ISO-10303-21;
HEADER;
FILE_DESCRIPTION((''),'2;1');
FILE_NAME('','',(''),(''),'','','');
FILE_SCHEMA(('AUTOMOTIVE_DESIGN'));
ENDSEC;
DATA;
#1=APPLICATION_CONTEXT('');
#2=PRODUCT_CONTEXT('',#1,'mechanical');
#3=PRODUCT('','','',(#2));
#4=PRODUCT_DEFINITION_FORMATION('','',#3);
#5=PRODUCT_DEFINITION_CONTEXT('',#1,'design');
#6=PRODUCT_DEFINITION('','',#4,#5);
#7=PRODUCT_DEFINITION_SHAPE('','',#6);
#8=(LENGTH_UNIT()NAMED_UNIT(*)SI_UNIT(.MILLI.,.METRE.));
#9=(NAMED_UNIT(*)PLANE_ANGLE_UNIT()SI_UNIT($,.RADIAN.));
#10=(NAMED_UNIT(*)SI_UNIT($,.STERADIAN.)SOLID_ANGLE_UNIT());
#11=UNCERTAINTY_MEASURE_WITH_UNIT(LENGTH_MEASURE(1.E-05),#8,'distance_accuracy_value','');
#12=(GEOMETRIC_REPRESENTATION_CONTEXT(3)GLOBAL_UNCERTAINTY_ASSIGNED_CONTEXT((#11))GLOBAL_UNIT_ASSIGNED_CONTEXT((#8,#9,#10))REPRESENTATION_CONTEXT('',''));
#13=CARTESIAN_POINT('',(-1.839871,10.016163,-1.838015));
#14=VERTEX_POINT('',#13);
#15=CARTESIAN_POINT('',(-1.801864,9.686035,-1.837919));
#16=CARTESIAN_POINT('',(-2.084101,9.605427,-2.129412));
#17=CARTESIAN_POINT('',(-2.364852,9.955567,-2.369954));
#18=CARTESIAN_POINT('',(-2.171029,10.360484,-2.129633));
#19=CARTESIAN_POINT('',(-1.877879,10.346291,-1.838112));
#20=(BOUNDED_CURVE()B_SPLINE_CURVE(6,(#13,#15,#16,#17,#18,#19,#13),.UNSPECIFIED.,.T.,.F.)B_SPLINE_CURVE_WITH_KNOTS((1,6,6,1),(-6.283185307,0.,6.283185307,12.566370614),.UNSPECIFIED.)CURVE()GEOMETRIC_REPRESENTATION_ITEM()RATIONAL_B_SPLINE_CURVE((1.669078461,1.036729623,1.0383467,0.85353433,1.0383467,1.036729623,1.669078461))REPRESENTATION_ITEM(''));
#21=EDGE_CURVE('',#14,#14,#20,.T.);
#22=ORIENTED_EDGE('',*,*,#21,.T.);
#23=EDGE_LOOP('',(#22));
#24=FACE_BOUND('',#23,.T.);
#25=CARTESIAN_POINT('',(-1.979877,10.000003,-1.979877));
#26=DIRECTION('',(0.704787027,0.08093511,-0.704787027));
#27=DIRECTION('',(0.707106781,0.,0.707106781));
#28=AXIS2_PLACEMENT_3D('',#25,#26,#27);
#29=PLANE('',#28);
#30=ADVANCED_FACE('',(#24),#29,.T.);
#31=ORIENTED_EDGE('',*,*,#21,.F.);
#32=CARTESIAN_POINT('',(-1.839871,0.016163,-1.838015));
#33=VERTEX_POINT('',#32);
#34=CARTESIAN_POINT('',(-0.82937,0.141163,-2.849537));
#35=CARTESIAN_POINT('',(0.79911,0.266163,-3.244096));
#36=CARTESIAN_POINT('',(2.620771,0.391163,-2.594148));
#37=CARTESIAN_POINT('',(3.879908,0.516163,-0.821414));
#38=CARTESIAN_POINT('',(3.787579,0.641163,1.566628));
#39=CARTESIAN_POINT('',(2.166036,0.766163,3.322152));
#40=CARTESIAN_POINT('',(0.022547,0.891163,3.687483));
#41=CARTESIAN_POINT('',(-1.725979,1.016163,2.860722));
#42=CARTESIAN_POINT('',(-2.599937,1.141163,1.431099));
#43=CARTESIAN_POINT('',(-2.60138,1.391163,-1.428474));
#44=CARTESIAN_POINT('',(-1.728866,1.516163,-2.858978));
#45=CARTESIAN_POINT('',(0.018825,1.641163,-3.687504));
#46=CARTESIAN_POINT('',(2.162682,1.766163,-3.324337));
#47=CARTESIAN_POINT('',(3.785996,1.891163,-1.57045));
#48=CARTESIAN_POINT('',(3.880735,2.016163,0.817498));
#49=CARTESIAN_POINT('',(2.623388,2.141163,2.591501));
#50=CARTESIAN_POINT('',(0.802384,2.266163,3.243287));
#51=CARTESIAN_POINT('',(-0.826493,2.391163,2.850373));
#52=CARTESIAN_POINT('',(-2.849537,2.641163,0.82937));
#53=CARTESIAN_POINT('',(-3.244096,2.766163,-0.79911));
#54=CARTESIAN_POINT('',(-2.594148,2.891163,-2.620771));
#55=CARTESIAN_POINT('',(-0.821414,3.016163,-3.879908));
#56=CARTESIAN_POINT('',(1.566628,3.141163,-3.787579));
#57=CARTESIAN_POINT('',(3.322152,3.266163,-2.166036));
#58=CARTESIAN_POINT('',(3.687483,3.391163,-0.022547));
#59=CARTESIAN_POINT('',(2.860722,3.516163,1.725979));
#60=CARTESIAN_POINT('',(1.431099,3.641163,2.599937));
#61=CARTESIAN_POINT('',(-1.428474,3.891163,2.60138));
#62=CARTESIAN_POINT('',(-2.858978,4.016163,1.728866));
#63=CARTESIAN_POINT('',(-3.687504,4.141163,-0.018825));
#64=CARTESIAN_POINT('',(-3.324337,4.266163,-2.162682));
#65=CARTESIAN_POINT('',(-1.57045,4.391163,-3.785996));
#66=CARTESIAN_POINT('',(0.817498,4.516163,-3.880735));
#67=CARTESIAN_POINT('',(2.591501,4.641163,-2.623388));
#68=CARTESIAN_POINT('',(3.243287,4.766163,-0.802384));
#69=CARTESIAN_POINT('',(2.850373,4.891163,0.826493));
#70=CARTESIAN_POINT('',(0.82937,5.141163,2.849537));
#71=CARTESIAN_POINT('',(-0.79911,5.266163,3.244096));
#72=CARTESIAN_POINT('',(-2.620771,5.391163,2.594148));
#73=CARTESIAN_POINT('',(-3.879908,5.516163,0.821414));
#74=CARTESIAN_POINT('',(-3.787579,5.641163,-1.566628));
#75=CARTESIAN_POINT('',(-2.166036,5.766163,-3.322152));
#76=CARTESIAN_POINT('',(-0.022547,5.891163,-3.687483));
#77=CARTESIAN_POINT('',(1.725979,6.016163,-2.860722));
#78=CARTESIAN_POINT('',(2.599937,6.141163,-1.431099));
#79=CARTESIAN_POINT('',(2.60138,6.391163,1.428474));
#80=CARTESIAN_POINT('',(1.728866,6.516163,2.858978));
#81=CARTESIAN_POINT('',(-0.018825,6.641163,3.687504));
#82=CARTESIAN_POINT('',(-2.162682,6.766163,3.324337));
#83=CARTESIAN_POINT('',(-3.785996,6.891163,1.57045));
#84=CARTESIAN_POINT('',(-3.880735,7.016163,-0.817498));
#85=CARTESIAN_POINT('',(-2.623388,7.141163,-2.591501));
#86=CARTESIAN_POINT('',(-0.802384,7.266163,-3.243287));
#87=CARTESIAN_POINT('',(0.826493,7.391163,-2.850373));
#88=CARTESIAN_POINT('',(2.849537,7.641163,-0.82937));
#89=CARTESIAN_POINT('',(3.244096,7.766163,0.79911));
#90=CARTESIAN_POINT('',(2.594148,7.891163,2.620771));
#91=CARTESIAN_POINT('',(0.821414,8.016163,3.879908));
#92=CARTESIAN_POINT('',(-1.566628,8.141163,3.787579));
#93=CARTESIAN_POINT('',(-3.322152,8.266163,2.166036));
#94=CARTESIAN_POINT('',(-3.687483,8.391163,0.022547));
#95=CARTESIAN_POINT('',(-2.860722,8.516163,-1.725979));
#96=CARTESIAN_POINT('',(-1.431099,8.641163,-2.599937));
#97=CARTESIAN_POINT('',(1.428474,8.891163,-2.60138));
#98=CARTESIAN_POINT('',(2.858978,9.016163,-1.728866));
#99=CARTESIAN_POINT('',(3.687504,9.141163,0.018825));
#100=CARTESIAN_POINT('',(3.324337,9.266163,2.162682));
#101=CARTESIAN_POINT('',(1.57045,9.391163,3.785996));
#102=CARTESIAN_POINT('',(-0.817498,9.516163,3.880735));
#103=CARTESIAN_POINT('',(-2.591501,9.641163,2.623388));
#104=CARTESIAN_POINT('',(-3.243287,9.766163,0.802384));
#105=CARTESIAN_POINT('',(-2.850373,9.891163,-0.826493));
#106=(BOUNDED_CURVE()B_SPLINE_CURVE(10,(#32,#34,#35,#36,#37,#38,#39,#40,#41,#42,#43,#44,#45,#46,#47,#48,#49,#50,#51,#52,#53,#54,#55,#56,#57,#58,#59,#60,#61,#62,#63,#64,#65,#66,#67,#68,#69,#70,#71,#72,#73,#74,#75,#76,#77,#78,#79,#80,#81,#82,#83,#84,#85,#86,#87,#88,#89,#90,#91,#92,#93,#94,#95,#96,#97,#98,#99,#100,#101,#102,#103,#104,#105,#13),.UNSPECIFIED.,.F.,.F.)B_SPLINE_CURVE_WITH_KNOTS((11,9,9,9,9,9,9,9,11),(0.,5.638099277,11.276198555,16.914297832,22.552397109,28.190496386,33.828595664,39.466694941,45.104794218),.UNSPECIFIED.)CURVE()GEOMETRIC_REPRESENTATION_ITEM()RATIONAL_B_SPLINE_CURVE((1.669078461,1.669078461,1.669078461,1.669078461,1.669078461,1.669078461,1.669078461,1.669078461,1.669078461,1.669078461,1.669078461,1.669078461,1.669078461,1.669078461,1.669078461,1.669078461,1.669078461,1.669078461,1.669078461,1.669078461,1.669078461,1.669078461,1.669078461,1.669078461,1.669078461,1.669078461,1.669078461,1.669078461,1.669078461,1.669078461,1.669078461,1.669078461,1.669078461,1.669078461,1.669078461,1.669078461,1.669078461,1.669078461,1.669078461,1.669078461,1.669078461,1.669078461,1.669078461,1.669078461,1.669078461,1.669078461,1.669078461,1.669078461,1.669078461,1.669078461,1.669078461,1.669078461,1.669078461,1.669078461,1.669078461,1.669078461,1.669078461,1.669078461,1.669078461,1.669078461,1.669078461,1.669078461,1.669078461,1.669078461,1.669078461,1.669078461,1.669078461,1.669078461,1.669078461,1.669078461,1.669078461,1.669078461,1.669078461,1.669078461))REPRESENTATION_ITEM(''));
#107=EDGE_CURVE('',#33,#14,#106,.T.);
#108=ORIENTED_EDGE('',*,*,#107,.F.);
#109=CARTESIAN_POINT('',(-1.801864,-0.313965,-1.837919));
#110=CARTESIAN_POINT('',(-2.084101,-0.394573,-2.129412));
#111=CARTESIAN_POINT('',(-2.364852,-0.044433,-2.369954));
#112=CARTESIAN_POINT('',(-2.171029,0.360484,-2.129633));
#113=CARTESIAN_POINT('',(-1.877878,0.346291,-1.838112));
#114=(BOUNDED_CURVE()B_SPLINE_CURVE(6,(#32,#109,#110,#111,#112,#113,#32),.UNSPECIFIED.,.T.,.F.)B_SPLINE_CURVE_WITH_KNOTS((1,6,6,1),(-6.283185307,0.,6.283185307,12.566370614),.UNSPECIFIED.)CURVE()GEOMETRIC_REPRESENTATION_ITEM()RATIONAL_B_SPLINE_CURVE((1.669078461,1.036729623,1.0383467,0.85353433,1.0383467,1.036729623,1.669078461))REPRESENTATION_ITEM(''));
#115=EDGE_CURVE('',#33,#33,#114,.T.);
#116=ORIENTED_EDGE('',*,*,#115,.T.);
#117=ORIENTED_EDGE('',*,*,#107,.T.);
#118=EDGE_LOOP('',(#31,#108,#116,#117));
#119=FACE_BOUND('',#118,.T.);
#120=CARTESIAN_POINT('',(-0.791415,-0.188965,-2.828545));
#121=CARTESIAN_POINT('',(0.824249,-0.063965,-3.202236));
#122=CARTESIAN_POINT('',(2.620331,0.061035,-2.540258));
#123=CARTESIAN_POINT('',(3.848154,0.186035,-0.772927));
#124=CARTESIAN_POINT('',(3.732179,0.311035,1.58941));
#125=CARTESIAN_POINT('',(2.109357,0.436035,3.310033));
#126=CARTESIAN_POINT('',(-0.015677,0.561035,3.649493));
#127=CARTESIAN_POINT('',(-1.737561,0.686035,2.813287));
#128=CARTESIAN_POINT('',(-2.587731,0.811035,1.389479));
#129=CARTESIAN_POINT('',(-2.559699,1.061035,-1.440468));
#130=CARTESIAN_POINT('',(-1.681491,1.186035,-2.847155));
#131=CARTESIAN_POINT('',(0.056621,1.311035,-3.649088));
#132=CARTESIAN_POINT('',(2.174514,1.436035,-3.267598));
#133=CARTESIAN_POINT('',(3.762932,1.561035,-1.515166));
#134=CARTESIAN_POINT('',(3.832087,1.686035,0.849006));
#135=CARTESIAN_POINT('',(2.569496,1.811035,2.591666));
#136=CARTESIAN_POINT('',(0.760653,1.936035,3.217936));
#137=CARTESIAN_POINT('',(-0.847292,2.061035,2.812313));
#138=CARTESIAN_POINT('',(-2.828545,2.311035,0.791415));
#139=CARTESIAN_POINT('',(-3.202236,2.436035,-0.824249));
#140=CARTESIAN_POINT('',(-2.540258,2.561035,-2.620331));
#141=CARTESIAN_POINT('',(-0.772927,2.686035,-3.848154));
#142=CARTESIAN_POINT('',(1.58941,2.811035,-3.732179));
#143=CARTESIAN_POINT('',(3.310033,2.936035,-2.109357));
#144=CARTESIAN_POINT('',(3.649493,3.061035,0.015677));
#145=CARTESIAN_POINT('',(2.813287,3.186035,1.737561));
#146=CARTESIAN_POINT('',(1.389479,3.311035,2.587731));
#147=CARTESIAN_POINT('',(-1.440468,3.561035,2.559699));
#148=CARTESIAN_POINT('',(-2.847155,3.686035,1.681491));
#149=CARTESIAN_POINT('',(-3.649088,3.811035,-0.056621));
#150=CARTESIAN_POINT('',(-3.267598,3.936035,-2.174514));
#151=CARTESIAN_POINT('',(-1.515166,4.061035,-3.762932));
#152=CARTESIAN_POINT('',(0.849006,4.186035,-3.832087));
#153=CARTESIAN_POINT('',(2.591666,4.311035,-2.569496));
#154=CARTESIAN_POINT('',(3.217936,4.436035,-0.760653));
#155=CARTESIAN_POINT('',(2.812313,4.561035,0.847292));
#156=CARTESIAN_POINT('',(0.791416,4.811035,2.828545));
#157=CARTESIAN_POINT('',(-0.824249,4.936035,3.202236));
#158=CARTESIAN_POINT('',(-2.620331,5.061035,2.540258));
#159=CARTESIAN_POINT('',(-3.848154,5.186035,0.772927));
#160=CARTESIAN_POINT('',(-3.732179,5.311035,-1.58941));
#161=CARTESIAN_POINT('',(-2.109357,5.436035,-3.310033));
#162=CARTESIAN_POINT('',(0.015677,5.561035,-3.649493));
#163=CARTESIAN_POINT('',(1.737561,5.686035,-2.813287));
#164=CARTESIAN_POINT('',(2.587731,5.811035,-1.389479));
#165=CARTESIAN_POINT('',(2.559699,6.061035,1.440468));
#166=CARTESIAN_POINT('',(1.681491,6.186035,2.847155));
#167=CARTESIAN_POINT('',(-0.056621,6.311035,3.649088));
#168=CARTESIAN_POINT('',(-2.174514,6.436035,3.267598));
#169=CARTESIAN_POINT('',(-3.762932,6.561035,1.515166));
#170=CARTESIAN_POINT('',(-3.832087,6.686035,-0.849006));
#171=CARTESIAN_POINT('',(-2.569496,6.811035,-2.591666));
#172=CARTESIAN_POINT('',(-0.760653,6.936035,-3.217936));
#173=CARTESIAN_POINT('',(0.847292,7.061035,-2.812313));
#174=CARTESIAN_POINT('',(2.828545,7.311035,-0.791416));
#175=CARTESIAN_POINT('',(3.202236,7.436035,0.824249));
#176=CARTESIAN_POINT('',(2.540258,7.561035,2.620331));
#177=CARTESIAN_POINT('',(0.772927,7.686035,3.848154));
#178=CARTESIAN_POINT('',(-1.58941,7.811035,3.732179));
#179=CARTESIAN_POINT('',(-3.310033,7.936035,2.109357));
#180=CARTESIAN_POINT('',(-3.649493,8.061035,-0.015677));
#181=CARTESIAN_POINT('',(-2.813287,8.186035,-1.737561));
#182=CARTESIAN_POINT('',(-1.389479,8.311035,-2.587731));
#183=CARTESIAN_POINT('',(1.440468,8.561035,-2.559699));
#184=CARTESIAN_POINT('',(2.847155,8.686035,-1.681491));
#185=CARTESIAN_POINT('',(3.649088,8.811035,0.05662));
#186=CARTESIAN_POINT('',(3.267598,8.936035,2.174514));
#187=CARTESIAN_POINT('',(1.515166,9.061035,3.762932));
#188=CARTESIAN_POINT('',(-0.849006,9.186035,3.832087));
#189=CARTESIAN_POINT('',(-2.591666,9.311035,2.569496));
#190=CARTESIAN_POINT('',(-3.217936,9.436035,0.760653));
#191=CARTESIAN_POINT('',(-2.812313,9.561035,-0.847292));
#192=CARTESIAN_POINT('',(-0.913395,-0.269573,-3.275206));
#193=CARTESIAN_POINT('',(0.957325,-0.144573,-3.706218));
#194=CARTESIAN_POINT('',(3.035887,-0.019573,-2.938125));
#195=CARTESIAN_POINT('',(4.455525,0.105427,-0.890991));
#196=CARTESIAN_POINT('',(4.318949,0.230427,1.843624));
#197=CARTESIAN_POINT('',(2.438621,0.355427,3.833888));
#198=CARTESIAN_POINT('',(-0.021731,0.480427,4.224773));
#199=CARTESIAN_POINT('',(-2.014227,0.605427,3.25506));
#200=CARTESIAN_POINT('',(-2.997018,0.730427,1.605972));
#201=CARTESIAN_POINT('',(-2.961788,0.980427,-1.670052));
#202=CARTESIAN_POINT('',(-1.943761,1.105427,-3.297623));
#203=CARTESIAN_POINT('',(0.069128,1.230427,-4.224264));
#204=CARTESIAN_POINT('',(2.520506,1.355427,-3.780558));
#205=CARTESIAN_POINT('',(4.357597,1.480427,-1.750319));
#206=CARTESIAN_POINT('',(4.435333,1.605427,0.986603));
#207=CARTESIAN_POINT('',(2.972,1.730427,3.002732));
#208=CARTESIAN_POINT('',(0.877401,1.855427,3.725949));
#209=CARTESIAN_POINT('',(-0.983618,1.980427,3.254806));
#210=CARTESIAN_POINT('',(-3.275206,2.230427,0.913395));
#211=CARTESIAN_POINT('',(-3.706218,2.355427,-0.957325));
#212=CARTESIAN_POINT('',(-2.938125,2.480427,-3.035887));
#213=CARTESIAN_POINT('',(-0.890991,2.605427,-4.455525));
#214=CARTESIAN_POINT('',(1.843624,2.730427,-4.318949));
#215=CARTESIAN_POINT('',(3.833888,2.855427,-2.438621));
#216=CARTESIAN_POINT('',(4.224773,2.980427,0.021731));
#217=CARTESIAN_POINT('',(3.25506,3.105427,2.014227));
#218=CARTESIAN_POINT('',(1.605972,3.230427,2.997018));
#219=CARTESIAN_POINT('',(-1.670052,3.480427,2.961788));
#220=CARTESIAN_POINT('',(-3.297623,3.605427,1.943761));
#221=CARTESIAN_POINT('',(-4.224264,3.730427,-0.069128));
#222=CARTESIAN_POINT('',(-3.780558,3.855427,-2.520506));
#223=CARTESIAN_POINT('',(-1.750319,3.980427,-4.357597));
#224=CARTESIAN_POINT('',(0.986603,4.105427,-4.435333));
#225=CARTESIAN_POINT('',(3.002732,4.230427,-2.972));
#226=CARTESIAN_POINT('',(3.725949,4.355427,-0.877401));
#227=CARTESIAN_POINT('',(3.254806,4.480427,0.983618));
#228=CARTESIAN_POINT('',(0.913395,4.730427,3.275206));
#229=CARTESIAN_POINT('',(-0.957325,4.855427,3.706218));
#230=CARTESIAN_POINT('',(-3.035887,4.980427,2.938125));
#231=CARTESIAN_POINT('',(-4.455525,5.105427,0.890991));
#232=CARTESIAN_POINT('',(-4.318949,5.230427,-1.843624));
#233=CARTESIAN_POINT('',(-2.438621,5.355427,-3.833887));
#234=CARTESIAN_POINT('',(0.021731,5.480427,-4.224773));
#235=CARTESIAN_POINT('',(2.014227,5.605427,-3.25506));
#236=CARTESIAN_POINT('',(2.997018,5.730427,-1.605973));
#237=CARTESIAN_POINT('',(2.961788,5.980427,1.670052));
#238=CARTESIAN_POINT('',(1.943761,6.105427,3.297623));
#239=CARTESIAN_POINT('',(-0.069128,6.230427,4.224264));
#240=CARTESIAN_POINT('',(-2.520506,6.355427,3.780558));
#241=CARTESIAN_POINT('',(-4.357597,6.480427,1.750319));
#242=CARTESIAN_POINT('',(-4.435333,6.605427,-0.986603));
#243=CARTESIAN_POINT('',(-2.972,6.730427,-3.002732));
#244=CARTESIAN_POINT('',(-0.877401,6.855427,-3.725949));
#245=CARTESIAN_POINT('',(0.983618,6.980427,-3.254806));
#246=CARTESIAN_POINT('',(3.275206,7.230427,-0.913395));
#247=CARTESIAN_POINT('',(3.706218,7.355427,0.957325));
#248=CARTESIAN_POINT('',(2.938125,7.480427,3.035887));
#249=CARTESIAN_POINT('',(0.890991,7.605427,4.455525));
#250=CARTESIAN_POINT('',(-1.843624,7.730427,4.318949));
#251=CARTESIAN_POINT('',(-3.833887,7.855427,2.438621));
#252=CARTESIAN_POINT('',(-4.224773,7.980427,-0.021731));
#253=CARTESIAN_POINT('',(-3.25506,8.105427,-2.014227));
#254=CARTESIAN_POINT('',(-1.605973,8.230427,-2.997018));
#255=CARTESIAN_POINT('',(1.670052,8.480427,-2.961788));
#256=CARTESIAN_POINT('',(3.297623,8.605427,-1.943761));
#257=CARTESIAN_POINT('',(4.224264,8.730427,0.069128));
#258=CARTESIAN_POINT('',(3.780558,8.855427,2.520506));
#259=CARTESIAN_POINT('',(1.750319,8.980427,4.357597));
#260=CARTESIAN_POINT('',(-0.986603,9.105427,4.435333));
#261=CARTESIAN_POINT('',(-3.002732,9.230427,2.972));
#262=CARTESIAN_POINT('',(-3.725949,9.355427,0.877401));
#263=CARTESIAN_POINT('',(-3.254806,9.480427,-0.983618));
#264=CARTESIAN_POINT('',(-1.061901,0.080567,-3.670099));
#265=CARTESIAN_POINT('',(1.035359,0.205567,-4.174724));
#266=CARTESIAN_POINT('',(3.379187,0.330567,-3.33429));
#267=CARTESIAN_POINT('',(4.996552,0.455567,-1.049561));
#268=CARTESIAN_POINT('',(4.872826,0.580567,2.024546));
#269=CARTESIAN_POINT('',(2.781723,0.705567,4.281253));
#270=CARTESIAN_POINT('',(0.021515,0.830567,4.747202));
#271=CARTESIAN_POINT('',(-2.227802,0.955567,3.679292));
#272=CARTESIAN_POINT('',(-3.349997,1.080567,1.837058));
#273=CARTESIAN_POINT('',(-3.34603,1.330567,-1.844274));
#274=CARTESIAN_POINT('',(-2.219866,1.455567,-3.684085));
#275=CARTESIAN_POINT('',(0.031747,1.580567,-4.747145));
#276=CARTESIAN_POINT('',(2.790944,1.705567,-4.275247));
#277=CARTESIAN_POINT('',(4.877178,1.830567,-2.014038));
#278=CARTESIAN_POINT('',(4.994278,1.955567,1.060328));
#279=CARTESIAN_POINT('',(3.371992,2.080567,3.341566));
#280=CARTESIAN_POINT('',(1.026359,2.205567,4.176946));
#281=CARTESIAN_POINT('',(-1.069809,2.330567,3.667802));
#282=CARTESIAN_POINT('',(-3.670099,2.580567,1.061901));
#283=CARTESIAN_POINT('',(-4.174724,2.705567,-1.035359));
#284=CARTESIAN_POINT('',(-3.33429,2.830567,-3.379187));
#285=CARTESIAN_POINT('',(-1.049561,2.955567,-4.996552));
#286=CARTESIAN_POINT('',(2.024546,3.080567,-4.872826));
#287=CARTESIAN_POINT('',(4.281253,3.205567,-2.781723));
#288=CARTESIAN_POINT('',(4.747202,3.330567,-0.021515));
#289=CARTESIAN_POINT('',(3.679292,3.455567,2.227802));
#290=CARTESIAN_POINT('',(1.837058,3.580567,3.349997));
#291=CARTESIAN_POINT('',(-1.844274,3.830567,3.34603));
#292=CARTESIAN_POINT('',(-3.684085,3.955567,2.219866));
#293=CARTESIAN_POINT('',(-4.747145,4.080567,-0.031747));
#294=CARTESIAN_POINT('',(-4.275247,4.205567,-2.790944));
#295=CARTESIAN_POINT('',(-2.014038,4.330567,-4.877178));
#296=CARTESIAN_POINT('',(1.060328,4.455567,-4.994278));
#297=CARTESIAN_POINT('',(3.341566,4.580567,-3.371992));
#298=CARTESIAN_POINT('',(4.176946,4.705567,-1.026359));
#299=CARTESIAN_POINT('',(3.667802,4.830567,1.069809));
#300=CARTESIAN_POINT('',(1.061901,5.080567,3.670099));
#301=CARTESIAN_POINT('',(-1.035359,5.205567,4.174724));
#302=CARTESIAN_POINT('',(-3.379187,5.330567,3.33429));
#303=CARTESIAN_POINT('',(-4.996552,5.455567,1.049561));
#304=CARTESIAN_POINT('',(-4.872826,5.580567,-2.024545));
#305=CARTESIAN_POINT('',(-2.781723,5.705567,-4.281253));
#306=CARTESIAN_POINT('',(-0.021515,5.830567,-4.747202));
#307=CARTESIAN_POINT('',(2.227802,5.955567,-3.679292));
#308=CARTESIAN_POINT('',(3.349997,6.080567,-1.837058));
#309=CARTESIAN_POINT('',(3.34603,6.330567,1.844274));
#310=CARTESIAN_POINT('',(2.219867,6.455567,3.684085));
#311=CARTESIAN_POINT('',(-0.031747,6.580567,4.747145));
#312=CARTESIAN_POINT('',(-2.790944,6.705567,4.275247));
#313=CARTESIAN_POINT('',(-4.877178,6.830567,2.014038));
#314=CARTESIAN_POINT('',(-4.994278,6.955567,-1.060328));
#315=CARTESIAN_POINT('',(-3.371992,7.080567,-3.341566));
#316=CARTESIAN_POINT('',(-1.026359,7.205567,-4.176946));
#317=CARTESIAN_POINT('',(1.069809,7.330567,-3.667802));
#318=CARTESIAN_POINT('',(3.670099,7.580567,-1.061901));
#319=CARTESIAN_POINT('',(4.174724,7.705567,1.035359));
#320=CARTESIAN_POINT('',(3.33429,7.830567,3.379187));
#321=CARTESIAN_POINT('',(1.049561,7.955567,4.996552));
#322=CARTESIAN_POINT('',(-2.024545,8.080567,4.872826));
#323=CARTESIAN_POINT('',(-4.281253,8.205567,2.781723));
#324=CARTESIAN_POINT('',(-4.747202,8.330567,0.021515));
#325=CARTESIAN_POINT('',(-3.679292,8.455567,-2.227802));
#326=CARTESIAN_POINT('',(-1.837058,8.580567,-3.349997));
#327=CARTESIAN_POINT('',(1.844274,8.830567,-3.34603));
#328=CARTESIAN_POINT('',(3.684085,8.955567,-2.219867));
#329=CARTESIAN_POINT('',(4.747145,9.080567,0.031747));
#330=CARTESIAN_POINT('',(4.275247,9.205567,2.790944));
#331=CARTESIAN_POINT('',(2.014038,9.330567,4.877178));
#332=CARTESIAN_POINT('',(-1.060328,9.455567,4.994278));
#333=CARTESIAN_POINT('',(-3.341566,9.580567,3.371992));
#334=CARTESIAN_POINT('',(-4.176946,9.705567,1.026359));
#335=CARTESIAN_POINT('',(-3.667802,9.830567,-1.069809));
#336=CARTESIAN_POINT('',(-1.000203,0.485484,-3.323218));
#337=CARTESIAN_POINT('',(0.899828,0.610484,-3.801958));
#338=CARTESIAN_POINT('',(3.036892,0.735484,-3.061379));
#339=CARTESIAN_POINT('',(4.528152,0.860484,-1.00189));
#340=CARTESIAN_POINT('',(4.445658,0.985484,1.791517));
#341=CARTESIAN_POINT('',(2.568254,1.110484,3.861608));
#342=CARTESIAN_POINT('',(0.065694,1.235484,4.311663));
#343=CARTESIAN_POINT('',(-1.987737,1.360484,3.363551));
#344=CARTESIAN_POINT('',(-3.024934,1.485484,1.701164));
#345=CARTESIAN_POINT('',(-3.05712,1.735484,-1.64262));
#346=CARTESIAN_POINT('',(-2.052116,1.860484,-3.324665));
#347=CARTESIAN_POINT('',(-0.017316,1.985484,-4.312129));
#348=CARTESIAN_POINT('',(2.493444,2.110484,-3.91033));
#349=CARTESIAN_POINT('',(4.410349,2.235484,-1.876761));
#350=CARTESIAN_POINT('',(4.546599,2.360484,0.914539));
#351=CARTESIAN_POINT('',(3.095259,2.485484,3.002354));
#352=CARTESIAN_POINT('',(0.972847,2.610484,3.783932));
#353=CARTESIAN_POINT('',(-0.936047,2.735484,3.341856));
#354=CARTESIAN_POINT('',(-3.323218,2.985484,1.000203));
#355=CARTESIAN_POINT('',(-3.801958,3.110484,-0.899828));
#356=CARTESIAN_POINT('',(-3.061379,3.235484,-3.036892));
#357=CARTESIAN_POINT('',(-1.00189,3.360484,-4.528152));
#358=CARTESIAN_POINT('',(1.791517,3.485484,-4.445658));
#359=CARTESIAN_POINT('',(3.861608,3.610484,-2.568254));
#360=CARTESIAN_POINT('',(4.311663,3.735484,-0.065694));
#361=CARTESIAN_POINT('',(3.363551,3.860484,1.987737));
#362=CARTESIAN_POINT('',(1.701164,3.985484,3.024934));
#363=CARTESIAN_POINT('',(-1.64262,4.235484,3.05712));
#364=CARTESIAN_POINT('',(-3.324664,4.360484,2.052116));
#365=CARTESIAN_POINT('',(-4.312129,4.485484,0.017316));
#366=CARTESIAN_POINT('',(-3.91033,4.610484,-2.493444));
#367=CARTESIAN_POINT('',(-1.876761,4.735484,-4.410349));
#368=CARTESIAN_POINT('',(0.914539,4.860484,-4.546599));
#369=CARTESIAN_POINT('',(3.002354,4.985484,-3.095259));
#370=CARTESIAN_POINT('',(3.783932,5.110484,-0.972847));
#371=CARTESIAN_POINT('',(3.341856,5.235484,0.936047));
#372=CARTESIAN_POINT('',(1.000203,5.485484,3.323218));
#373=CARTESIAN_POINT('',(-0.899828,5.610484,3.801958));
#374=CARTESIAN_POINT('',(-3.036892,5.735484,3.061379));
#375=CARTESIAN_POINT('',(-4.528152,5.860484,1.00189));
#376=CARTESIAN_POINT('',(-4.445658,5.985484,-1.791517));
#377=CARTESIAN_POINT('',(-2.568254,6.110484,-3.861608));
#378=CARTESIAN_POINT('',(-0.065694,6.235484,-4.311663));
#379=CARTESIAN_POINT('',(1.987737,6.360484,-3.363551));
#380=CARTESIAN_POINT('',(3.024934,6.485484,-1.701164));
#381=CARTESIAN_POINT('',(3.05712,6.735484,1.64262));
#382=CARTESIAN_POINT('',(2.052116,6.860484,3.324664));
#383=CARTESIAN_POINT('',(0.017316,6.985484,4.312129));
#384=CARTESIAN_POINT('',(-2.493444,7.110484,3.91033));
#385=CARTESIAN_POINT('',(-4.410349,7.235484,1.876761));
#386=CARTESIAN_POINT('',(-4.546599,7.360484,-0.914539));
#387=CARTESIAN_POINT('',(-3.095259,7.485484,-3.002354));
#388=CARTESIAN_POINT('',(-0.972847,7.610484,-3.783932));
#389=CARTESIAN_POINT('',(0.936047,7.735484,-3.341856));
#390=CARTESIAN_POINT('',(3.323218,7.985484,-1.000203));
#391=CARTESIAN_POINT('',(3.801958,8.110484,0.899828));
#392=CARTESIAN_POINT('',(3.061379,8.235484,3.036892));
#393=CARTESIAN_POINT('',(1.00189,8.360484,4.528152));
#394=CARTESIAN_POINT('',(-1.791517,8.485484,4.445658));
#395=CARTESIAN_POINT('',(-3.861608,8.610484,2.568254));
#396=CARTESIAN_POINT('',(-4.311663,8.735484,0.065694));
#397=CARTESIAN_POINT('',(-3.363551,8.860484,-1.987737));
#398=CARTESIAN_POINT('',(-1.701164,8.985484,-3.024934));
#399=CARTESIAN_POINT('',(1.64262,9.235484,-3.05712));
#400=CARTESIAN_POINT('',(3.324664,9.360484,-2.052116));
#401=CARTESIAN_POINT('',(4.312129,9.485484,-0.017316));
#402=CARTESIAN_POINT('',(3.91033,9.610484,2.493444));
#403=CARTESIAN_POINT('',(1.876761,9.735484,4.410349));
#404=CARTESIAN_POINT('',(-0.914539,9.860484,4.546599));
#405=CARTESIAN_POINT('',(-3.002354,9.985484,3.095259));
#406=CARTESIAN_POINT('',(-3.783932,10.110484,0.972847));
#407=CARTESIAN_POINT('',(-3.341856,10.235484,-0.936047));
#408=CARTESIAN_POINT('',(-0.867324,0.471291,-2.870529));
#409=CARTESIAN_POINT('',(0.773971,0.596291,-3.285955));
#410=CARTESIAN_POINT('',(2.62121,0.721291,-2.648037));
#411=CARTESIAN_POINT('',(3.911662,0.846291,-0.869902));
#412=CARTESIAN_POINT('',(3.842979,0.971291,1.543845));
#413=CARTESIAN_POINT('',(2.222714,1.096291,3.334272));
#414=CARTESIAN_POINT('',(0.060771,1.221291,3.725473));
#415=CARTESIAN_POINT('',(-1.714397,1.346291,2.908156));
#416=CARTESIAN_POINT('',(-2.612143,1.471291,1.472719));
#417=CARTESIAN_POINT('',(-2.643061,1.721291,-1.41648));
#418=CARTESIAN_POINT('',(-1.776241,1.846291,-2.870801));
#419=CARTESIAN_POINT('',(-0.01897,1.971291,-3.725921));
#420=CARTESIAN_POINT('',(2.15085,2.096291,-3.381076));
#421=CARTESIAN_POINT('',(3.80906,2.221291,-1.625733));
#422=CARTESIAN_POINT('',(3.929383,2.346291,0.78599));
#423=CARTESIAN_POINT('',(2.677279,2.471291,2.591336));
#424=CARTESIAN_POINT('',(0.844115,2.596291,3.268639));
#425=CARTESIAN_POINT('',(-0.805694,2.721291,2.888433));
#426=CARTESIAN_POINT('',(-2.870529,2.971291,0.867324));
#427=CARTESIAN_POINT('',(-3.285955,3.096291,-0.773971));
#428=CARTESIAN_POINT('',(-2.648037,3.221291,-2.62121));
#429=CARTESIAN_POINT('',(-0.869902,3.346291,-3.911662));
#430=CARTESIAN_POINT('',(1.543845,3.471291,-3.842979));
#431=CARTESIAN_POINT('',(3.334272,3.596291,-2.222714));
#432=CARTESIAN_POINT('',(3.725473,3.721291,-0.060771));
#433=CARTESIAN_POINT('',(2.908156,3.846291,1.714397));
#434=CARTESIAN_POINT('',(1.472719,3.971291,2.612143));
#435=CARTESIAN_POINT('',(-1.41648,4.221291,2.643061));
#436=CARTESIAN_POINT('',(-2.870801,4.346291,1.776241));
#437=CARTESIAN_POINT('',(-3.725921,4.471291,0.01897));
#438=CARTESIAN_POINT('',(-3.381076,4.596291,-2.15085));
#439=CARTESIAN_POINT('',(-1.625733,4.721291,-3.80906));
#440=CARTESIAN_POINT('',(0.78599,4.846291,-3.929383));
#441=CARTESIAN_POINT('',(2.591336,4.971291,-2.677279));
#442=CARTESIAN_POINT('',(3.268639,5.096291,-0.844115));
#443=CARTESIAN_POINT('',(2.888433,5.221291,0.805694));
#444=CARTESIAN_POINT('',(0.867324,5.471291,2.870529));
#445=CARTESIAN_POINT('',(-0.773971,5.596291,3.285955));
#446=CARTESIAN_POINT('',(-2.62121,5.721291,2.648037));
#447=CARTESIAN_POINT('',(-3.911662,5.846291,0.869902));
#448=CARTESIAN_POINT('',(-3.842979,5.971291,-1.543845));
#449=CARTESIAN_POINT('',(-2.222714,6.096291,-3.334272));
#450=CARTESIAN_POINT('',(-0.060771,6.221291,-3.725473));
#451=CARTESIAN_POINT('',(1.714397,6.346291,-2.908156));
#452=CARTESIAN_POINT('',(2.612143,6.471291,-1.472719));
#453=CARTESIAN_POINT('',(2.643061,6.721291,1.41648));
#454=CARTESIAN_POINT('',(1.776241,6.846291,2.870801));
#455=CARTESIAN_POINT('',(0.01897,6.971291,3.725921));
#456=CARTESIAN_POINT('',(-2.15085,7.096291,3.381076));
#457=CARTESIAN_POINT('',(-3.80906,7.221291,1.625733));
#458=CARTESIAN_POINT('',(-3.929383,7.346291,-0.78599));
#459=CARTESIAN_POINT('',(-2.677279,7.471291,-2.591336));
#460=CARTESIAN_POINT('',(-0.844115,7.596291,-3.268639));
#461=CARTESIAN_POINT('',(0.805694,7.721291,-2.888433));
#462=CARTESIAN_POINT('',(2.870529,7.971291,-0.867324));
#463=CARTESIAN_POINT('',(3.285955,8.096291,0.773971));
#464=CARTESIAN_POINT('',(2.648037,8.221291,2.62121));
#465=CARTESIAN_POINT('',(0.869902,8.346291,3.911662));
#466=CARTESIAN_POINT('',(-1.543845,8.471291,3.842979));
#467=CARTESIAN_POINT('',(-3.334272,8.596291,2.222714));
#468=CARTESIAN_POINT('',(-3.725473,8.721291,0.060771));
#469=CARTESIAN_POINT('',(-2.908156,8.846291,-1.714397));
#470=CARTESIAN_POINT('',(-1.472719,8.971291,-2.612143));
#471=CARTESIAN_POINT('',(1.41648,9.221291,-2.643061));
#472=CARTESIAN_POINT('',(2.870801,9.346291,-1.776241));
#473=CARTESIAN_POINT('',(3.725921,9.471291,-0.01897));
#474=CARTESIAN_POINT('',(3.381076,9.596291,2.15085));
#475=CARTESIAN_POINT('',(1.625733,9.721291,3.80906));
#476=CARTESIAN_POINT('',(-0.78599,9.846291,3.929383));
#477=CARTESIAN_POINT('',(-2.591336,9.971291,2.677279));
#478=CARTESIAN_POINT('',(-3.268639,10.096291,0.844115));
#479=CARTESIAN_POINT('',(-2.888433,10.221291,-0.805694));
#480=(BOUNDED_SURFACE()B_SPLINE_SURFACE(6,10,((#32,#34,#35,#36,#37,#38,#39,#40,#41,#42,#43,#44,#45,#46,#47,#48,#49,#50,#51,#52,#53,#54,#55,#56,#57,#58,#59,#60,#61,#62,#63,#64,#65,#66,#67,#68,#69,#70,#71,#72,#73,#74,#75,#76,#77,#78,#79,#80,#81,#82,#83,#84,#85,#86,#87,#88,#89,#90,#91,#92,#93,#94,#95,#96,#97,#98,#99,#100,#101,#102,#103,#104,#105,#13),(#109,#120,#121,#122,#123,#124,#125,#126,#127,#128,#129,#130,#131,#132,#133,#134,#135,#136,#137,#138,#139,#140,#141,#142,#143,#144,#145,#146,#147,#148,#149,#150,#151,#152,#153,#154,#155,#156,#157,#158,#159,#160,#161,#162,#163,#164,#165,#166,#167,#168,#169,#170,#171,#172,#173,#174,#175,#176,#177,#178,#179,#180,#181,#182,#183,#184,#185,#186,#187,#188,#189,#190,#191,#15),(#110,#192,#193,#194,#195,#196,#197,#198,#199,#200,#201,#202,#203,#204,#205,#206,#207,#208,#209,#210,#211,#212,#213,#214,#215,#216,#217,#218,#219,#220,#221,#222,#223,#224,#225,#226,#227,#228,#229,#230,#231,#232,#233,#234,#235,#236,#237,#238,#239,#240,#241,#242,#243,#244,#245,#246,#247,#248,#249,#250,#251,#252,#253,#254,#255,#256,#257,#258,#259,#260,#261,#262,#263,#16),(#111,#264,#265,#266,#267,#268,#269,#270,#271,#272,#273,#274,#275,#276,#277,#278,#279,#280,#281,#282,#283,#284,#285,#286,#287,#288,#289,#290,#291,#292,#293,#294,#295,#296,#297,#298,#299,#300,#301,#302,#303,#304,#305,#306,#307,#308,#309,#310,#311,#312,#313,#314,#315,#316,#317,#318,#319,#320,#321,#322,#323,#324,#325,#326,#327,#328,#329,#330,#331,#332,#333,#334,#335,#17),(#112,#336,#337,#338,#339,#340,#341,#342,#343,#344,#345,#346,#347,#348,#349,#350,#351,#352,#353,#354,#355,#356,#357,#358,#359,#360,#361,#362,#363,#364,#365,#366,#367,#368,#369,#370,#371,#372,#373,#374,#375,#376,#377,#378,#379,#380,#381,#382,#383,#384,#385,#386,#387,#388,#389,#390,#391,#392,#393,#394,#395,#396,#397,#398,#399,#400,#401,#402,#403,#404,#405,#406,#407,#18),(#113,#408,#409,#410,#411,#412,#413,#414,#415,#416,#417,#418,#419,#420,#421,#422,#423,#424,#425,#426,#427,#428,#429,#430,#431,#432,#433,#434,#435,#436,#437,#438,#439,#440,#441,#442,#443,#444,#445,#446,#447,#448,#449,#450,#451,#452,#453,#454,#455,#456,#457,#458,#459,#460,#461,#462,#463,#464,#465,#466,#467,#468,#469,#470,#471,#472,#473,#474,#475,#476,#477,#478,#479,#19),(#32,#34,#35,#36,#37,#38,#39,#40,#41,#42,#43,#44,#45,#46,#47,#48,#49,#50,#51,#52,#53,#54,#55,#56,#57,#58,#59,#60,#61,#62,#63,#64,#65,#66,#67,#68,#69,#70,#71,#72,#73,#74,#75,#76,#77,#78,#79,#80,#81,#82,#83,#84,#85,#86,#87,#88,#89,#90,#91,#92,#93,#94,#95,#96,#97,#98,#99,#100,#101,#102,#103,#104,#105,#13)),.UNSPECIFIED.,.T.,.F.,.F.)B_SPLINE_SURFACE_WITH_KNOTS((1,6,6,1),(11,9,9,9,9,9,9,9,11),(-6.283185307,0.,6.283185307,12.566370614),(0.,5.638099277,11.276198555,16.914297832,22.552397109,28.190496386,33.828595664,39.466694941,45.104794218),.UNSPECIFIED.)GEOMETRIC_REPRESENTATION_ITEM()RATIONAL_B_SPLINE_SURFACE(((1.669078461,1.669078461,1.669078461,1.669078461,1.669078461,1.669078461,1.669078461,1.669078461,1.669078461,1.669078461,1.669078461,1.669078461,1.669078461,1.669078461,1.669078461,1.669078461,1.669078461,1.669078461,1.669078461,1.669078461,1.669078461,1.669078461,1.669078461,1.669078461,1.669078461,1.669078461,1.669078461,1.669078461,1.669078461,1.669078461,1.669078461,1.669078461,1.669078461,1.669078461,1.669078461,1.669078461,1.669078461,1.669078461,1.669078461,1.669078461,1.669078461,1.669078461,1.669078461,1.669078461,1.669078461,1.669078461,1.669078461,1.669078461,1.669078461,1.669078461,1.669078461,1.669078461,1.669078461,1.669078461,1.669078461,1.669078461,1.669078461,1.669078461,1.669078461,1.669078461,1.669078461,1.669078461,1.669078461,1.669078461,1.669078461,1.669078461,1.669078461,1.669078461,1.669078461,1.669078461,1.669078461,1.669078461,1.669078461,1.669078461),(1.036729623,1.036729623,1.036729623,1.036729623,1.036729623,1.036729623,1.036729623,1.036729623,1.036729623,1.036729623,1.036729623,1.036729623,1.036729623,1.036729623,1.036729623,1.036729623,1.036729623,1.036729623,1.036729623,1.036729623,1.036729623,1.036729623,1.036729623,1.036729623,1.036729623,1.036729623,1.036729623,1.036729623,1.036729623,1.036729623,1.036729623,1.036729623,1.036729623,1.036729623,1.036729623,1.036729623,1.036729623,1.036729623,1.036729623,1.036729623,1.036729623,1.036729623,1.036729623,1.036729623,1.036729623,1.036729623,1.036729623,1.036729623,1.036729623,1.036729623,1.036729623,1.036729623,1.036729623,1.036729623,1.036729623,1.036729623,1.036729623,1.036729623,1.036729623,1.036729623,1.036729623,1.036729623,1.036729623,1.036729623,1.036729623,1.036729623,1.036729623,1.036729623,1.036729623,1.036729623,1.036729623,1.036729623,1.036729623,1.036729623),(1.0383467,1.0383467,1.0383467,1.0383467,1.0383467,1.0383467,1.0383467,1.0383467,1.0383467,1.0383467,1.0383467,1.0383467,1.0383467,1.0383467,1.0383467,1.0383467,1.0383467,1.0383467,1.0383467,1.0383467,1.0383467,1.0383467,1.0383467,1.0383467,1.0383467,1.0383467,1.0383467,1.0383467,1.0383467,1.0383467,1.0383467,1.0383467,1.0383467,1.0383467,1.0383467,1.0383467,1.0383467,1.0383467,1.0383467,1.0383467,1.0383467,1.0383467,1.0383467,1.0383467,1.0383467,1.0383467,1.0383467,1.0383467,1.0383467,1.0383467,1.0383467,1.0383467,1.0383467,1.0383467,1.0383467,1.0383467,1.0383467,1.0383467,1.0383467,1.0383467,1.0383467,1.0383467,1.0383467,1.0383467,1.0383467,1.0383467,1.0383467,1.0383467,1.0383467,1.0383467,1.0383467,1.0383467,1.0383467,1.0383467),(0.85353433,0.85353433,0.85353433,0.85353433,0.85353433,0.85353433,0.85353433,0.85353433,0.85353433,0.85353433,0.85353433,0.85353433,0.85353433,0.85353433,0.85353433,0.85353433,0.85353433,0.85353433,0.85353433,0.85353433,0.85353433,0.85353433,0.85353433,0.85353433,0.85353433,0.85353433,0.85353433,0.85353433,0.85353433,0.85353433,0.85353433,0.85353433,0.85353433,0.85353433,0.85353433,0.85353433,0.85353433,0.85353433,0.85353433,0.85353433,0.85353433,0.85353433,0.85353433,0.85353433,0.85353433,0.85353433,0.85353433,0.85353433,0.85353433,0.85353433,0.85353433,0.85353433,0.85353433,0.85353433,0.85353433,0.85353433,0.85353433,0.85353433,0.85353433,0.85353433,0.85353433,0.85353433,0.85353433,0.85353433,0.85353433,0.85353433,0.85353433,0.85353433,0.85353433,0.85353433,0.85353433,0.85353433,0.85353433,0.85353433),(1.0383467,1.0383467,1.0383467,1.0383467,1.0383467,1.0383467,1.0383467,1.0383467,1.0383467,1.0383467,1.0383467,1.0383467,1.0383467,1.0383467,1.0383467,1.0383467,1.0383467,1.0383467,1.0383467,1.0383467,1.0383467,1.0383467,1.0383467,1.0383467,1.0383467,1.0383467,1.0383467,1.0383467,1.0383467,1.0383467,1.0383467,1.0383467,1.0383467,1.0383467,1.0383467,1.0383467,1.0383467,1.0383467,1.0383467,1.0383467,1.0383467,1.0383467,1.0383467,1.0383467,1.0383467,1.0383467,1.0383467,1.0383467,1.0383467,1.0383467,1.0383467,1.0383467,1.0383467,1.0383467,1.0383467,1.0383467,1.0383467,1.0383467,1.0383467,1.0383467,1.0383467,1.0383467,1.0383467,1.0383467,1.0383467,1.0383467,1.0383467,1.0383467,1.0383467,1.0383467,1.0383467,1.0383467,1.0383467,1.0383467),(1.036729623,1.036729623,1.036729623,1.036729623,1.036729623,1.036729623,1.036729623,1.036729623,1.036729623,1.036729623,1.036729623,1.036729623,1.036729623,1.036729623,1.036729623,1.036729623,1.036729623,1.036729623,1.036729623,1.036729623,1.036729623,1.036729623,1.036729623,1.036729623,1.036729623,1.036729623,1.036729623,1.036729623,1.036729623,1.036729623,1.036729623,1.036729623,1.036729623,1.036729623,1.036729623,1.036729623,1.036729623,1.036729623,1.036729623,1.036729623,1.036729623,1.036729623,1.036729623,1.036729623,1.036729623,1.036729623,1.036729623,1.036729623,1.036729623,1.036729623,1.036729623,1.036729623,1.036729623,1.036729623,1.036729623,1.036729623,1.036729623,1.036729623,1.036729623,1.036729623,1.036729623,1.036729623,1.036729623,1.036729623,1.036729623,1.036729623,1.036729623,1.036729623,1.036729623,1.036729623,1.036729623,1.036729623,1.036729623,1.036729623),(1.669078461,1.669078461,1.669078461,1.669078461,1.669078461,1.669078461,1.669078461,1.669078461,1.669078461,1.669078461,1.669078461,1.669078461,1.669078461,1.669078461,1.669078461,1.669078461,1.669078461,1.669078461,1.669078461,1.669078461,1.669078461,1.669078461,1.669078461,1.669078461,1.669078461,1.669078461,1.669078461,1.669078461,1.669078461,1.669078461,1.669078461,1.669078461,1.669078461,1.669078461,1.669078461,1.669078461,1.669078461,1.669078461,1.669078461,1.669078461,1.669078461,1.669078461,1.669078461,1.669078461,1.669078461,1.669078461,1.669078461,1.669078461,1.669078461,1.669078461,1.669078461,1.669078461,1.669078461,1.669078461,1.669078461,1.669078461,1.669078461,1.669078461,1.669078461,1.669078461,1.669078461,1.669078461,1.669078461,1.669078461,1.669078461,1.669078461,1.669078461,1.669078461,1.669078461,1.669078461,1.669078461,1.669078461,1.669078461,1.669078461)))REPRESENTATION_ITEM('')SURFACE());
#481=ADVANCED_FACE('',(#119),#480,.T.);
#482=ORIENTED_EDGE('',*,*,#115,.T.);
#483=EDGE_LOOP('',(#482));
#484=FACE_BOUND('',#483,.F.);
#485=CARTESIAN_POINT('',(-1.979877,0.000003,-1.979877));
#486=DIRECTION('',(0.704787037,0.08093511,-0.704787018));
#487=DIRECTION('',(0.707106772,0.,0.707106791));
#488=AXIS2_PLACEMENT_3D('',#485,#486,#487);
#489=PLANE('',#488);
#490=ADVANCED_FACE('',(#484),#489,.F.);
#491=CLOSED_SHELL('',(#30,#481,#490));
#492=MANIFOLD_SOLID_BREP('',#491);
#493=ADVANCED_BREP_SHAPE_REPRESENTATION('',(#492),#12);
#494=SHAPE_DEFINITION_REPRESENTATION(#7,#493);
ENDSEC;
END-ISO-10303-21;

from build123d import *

# Parameters (mm, degrees)
SWEEP1_PITCH       = 1.428571429
SWEEP1_HEIGHT      = 10
SWEEP1_RADIUS      = 2.8
SWEEP1_START_ANGLE = -135
SKETCH2_R          = 0.2


with BuildPart() as part:
    # Sweep1: sweep along a helix
    with BuildLine() as sweep1_path:
        add(Helix(SWEEP1_PITCH, SWEEP1_HEIGHT, SWEEP1_RADIUS, center=(0, 0, 0), direction=(0, 1, 0), lefthand=True, mode=Mode.PRIVATE).rotate(Axis((0, 0, 0), (0, 1, 0)), SWEEP1_START_ANGLE))
    # Sketch2 → Sweep1 (sweep)
    with BuildSketch(Plane(origin=(-1.979898987, 10, -1.979898987), x_dir=(0.7001385575920928, 0.08081360418948051, 0.709418890043654), z_dir=(0.7047870274114748, 0.08093510971866495, -0.7047870274113484))):
        Circle(SKETCH2_R)
    sweep(path=sweep1_path.line, is_frenet=True)


solid = part.part
